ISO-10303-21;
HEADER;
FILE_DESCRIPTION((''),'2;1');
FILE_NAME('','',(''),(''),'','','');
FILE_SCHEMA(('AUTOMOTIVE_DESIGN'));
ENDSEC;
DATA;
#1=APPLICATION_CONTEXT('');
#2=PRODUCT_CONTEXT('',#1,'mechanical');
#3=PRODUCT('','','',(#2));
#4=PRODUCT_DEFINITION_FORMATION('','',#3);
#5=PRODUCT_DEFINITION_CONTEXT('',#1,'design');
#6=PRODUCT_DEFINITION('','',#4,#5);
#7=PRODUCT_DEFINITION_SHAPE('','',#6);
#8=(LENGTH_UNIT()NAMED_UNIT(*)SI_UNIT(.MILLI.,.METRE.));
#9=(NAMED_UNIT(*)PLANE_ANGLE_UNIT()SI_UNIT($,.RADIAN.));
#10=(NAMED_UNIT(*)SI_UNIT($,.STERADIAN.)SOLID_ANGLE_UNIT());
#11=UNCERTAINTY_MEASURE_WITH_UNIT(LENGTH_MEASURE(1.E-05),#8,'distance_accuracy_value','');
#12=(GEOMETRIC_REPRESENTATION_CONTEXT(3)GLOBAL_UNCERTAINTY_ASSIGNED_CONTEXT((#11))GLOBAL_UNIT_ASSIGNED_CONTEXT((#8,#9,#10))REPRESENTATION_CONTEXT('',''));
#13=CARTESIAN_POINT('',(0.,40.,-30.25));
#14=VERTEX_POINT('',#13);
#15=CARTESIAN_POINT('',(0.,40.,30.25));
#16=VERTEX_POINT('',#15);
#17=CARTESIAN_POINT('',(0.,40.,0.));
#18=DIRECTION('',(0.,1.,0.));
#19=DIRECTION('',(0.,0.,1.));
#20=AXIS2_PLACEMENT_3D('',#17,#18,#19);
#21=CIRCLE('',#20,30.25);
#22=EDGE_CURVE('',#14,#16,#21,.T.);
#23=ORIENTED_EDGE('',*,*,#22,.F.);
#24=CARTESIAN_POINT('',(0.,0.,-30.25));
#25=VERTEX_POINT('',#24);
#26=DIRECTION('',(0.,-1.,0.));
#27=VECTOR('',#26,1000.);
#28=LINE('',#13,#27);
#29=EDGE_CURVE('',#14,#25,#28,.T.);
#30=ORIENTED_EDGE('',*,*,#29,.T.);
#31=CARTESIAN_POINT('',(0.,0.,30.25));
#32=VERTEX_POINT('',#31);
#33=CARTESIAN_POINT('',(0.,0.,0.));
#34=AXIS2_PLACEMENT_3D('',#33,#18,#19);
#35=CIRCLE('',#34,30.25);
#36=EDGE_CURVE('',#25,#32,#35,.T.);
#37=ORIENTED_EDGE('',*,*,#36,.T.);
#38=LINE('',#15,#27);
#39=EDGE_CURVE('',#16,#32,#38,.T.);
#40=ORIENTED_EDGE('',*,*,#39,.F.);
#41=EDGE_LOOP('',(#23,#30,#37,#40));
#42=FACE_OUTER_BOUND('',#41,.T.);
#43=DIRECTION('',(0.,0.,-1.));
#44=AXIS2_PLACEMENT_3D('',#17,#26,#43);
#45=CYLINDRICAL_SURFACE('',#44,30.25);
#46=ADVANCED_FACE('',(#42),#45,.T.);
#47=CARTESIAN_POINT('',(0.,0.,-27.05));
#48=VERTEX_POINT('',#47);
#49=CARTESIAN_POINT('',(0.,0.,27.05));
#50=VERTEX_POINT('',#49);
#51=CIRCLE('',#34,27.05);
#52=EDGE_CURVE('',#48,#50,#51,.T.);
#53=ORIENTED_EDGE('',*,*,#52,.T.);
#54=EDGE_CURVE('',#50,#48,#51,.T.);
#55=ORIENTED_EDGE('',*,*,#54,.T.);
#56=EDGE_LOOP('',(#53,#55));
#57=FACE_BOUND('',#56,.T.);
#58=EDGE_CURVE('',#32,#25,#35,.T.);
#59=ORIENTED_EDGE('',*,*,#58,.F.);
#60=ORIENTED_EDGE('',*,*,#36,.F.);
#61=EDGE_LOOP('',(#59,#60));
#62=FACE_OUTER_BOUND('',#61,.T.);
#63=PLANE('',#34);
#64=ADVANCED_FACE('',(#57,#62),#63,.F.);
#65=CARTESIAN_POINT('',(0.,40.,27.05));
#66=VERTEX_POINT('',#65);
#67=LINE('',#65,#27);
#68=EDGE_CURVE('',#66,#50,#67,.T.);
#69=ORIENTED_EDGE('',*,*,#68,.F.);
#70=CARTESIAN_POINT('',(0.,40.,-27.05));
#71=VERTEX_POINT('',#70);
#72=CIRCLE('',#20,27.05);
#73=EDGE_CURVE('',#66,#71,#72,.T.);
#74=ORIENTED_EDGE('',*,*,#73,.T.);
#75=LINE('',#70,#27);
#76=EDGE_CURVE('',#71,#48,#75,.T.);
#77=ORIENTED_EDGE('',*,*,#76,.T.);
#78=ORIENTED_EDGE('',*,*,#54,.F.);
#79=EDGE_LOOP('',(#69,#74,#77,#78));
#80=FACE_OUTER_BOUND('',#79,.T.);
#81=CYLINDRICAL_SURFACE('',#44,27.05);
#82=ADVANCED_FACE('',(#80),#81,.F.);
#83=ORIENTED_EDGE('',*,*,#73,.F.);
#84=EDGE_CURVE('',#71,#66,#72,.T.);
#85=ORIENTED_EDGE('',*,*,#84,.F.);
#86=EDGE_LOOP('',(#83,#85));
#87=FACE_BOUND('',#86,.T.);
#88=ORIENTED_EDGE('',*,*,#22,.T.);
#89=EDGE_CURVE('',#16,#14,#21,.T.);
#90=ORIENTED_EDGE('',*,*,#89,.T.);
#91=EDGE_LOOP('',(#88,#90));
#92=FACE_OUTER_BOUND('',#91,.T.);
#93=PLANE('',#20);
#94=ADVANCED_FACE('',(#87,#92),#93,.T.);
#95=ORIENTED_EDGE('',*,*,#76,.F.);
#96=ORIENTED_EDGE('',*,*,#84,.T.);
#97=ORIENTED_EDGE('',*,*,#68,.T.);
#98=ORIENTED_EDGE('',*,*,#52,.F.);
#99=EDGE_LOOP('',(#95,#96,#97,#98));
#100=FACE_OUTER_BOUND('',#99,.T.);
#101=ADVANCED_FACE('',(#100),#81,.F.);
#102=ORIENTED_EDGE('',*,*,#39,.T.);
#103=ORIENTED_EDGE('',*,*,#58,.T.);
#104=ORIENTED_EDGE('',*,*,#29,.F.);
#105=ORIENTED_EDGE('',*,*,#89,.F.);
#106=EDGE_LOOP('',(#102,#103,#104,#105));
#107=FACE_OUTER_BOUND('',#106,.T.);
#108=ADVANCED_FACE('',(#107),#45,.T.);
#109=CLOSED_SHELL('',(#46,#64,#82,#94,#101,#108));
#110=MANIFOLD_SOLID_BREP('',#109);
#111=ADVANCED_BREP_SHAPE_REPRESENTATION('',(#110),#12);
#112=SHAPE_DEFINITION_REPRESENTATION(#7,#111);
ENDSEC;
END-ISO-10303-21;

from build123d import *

# Parameters (mm, degrees)
SKETCH1_R           = 30.25
SKETCH1_R_2         = 27.05
BOSS_EXTRUDE1_DEPTH = 40


with BuildPart() as part:
    # Sketch1 → Boss-Extrude1 (new body)
    with BuildSketch(Plane(origin=(0, 0, 0), x_dir=(1, 0, 0), z_dir=(0, 1, 0))):
        with Locations(Location((0, 0, 0), (0, 0, 270))):
            Circle(SKETCH1_R)
        with Locations(Location((0, 0, 0), (0, 0, 270))):
            Circle(SKETCH1_R_2, mode=Mode.SUBTRACT)
    extrude(amount=BOSS_EXTRUDE1_DEPTH)


solid = part.part
